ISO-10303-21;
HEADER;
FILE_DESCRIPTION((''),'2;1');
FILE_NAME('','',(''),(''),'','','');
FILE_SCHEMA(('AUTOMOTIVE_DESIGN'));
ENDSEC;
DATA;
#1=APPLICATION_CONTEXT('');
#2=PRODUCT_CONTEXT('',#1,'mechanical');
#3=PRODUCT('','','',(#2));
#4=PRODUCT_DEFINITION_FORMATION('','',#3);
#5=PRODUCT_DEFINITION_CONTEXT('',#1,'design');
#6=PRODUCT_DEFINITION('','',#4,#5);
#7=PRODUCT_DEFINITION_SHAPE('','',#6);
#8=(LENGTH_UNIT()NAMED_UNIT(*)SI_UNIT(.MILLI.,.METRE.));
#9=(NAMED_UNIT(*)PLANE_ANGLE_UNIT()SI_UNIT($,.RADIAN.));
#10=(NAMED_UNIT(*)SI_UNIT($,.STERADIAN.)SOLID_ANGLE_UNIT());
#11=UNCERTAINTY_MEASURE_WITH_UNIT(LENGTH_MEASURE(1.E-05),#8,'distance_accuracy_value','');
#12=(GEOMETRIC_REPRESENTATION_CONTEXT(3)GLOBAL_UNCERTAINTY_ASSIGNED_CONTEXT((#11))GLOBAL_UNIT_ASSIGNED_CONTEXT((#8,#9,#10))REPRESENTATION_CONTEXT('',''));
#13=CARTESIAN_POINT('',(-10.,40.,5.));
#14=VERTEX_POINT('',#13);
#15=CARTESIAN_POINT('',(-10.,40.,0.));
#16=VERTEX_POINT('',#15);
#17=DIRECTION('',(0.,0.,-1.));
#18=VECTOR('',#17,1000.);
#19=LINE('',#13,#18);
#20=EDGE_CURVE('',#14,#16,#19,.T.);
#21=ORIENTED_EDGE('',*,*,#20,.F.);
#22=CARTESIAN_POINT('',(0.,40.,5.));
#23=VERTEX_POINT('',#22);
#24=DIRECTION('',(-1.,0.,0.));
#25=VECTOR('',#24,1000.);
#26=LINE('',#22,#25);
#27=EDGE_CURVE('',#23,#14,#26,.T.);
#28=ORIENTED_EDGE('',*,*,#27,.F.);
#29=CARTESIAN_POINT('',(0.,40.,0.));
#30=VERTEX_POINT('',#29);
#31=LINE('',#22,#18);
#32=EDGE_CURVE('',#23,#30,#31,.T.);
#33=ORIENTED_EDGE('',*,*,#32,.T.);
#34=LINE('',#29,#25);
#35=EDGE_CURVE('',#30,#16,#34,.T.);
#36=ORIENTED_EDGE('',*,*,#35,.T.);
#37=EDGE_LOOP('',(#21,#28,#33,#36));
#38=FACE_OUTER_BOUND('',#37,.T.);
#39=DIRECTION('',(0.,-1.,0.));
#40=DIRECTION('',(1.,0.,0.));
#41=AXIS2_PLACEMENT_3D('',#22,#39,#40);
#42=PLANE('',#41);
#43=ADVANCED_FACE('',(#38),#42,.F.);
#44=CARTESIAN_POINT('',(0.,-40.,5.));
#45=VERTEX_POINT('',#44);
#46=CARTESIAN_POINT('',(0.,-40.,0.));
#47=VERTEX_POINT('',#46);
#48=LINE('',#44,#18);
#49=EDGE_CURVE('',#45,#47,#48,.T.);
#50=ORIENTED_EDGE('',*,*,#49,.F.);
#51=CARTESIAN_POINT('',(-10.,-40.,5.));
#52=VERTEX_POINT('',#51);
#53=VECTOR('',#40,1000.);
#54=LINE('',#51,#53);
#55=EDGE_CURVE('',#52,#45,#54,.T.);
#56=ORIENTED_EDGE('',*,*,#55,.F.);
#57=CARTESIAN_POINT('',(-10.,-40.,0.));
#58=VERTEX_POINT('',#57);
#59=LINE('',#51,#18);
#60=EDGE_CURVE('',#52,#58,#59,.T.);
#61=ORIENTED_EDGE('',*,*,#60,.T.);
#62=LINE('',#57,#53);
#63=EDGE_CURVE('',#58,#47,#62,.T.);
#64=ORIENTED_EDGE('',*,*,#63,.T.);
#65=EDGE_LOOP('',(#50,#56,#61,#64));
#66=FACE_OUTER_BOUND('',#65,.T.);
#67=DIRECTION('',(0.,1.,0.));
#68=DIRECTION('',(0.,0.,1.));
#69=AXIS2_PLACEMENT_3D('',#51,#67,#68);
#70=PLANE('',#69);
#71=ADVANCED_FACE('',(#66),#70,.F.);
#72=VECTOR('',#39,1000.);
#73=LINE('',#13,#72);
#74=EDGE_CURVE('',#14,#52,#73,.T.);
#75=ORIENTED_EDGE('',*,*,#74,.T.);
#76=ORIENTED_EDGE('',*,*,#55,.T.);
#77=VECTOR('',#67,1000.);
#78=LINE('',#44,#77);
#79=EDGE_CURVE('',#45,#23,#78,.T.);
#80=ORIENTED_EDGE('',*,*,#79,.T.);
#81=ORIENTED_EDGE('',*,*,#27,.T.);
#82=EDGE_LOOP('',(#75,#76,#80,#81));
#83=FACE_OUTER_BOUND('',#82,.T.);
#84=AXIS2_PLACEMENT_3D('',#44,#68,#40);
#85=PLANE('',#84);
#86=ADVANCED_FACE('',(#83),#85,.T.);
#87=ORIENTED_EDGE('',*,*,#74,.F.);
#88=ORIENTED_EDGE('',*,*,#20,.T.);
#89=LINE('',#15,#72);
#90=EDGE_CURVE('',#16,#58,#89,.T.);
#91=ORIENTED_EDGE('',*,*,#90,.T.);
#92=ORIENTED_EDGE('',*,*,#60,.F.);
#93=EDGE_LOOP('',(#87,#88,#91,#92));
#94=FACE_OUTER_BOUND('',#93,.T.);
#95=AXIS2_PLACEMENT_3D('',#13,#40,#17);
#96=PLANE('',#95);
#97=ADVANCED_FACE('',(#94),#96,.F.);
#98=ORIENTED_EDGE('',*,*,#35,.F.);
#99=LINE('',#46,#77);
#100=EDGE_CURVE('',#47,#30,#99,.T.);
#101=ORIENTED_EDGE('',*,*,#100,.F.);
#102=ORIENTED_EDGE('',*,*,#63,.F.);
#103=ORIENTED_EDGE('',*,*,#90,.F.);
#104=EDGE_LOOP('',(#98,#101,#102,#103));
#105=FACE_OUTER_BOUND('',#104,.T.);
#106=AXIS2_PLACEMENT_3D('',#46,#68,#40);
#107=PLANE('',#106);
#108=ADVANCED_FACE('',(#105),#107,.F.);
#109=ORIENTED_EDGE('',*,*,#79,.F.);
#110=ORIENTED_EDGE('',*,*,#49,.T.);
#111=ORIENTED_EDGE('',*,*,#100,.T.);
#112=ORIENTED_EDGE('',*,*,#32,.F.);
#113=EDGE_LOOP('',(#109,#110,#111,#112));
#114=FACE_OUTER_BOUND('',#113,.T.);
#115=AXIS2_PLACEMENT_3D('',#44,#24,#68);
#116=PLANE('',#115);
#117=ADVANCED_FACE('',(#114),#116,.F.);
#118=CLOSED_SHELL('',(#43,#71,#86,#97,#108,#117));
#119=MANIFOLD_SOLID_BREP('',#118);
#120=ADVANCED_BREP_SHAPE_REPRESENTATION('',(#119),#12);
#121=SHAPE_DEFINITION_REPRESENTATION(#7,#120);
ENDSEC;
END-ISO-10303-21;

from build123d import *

# Parameters (mm, degrees)
SKETCH1_W          = 10
SKETCH1_H          = 80
BASE_EXTRUDE_DEPTH = 5


with BuildPart() as part:
    # Sketch1 → Base-Extrude (new body)
    with BuildSketch(Plane.XY):
        with Locations((-5, 0)):
            Rectangle(SKETCH1_W, SKETCH1_H)
    extrude(amount=BASE_EXTRUDE_DEPTH)


solid = part.part
